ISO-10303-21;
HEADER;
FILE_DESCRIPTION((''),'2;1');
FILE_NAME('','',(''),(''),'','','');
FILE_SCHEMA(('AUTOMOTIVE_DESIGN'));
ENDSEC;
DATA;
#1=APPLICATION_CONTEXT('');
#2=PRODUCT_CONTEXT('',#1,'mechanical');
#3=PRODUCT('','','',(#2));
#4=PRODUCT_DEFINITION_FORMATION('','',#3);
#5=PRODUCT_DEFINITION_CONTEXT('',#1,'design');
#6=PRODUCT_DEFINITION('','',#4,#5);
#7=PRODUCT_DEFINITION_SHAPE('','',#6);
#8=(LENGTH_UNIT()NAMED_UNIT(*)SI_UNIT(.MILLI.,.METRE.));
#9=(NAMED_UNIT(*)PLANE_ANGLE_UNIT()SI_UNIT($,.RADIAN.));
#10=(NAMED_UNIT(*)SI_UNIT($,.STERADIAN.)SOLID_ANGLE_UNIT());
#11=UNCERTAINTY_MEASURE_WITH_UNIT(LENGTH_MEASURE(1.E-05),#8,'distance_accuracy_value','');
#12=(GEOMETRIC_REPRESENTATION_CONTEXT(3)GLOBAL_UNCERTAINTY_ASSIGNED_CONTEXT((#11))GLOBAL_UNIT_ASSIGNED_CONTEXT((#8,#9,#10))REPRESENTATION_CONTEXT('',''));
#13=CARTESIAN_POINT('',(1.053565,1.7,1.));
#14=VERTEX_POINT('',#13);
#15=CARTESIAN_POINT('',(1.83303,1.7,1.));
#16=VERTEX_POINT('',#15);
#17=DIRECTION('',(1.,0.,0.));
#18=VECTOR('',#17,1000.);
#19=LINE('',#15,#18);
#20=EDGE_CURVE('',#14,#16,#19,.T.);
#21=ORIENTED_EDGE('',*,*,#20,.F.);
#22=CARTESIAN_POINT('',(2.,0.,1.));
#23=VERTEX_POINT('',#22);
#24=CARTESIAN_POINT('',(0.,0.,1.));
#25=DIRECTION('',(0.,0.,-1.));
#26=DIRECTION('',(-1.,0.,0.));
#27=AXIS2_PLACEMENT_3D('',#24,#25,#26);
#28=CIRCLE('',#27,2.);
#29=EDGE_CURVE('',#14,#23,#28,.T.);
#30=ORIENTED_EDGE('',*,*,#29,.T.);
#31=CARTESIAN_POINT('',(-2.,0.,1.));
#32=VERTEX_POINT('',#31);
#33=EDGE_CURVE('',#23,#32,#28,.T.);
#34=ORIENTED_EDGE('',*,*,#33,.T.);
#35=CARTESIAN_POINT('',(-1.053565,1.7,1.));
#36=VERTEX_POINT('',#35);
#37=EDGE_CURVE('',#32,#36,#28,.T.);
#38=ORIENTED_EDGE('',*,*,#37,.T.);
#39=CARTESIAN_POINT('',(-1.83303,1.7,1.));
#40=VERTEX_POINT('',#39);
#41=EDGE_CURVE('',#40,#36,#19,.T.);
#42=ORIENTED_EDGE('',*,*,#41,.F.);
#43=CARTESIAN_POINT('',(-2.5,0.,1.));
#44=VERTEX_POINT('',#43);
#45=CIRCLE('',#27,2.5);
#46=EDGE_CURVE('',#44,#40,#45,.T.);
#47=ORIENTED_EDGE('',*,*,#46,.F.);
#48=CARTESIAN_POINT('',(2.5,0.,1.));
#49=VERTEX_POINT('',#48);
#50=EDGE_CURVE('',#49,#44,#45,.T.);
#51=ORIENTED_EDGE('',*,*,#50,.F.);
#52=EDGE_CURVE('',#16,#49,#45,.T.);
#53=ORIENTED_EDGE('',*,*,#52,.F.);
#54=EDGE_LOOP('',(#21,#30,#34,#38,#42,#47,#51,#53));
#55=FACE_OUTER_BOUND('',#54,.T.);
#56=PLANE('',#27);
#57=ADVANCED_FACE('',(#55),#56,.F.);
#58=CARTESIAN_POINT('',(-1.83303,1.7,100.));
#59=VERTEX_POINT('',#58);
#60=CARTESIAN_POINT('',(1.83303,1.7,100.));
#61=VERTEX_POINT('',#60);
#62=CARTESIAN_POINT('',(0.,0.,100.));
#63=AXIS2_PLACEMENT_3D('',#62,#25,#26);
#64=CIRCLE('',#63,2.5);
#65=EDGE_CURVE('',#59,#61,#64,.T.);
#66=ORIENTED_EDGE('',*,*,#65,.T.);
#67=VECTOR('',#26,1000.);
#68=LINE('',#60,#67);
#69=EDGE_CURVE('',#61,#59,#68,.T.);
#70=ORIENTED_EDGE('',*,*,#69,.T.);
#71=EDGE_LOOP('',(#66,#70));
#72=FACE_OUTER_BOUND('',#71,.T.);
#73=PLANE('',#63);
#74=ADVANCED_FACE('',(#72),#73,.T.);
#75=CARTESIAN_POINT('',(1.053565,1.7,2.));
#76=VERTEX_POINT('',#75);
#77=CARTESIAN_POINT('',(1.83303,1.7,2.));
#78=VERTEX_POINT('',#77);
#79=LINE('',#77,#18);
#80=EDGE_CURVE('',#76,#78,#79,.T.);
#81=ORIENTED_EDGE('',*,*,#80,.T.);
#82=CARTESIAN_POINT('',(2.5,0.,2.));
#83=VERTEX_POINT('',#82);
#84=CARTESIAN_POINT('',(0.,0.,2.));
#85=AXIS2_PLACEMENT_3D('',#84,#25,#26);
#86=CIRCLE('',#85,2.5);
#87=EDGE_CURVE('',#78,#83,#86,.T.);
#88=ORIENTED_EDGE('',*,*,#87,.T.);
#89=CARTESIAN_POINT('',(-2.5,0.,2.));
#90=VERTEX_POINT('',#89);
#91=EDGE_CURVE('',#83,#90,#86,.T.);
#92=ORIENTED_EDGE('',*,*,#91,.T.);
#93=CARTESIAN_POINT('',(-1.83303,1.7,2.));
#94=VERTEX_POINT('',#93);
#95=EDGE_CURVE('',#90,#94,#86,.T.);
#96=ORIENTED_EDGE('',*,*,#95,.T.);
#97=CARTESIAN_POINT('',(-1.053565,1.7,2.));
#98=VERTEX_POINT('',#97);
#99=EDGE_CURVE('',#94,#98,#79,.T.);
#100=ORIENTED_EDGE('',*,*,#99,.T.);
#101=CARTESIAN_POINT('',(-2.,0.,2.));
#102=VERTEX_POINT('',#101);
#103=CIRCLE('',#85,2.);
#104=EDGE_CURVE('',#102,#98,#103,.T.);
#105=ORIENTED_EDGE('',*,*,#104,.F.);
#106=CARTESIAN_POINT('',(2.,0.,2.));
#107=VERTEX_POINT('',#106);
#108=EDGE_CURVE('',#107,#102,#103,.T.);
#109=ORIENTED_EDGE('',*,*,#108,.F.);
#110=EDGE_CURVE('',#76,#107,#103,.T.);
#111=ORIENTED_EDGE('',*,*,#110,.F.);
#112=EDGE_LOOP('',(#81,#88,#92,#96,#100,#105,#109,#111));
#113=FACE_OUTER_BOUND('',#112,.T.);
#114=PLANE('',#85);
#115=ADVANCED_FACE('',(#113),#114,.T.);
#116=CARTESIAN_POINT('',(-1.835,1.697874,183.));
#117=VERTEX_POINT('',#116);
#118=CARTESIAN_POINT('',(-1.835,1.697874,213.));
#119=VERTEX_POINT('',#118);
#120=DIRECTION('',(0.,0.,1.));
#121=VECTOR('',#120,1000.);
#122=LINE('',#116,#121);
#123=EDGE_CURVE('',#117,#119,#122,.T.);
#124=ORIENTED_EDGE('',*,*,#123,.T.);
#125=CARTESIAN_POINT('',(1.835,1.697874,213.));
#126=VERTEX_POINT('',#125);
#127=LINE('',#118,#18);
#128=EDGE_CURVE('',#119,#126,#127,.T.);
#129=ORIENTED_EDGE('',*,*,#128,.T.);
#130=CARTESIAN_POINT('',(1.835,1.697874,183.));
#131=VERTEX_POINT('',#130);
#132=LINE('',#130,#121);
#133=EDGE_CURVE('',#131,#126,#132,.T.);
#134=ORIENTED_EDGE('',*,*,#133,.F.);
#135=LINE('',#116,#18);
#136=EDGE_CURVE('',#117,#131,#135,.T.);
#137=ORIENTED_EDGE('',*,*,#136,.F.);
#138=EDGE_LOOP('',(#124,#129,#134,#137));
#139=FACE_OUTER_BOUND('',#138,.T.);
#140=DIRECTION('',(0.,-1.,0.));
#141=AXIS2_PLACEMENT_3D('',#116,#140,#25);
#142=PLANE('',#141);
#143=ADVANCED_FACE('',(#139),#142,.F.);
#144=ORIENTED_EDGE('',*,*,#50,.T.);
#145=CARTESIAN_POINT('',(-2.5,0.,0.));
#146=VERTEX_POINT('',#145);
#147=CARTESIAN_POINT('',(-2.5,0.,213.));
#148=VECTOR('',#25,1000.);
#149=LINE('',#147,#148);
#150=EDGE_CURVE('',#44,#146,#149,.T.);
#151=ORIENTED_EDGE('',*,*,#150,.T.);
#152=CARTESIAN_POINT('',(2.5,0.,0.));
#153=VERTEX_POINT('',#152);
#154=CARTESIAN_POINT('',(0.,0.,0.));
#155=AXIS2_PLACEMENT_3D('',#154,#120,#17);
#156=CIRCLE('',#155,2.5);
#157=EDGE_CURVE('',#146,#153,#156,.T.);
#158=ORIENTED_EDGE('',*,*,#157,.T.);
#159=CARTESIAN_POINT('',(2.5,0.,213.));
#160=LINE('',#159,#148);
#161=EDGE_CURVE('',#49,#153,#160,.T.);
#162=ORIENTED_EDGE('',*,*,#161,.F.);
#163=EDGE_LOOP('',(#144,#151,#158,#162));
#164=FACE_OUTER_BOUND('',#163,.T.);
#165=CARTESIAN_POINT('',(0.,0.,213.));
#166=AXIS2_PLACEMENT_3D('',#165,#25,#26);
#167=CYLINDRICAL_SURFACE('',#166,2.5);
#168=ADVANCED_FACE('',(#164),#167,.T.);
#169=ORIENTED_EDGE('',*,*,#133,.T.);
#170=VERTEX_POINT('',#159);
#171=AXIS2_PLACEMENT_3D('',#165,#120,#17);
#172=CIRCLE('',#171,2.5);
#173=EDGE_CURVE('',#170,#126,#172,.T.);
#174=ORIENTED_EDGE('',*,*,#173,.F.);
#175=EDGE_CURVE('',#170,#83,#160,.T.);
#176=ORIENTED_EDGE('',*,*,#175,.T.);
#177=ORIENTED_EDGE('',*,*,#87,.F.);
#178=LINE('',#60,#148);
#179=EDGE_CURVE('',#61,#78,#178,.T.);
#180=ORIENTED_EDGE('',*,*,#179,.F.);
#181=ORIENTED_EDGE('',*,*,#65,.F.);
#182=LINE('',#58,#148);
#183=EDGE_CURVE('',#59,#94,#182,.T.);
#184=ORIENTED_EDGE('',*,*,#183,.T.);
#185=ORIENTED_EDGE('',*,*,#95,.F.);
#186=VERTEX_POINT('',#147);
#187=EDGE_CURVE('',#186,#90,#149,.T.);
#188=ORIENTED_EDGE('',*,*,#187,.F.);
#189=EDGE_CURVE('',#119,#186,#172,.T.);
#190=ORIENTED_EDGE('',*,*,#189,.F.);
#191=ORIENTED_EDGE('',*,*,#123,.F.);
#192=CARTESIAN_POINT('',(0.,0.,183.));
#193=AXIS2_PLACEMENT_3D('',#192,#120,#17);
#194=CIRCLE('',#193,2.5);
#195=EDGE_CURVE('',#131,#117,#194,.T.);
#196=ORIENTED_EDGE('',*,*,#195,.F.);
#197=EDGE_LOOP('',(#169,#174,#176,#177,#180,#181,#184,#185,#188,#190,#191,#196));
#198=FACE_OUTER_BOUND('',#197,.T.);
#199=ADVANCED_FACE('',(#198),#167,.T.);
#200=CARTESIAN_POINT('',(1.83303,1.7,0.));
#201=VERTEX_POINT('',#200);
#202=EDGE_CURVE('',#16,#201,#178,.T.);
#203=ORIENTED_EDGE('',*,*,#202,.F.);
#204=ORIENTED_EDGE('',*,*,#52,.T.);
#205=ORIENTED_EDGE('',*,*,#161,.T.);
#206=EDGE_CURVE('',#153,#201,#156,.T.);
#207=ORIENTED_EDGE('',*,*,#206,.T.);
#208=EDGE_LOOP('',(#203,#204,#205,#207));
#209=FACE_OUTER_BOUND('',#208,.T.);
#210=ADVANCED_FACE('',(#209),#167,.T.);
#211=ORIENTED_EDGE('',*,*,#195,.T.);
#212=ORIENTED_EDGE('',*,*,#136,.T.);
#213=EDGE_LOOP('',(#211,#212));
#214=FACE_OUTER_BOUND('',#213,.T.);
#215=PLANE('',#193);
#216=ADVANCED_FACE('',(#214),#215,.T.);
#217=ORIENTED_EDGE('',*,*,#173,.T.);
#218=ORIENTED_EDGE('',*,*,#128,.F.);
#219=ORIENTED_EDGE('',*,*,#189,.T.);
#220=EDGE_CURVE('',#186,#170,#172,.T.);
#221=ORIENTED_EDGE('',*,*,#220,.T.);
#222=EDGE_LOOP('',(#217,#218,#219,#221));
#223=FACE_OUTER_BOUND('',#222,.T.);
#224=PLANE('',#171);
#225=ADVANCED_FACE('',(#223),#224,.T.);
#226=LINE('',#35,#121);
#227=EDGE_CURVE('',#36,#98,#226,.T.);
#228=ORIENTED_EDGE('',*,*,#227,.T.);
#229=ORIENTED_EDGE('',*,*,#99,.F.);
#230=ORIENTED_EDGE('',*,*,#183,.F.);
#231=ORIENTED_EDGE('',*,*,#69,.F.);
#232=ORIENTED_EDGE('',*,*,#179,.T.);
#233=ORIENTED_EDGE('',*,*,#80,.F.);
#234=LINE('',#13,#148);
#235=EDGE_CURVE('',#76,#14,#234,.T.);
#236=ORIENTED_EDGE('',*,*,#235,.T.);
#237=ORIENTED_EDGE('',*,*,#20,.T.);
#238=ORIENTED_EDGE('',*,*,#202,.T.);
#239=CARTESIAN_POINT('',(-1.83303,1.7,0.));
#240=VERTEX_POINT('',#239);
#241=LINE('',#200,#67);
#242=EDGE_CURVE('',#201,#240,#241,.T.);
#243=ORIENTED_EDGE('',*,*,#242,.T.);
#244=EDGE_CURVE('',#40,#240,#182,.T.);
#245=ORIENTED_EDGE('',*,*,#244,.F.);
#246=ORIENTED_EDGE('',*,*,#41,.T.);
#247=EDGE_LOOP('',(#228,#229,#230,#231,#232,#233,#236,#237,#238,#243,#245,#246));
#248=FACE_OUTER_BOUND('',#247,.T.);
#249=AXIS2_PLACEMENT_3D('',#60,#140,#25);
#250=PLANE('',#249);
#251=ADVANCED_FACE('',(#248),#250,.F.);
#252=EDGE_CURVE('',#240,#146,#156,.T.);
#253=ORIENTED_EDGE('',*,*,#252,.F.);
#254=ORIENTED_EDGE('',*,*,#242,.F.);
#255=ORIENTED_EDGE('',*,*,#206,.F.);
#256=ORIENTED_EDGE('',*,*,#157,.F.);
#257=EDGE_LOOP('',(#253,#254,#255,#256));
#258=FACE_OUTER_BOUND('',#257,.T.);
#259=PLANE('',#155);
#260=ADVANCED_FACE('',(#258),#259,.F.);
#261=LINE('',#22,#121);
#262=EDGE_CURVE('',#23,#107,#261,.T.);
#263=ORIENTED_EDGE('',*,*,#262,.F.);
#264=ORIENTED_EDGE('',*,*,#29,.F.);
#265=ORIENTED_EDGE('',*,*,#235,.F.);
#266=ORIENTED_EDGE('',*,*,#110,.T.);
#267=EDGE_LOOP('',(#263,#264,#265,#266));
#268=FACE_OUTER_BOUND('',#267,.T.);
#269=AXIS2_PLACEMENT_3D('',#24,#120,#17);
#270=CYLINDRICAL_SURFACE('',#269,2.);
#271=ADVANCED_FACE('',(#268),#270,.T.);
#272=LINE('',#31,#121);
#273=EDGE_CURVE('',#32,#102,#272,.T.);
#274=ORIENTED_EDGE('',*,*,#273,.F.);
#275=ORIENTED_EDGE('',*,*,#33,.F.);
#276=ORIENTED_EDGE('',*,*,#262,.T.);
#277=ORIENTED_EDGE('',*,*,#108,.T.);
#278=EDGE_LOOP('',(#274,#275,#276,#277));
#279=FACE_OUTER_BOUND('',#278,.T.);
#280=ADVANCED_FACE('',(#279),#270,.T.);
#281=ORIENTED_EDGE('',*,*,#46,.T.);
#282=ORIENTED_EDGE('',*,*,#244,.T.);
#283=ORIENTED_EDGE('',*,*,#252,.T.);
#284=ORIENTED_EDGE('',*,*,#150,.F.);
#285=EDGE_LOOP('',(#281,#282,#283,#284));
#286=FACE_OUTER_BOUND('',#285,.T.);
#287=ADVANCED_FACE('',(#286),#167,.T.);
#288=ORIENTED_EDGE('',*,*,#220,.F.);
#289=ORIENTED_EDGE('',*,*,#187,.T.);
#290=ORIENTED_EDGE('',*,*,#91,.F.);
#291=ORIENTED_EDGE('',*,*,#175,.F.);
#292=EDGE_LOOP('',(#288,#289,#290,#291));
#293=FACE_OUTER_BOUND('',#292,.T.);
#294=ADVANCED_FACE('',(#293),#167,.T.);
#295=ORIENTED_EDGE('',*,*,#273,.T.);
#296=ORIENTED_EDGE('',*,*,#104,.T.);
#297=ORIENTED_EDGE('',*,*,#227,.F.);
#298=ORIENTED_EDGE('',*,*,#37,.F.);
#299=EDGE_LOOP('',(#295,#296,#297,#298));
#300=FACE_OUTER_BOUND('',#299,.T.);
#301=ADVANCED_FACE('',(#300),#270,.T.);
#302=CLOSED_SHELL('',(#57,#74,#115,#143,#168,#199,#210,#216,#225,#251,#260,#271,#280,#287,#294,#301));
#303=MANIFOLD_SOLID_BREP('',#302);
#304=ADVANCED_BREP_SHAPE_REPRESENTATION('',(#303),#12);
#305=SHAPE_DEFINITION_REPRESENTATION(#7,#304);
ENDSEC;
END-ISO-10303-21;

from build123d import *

# Parameters (mm, degrees)
SKETCH1_R           = 2.5
BOSS_EXTRUDE1_DEPTH = 213
CUT_EXTRUDE2_DEPTH  = 100
CUT_EXTRUDE3_START  = 1
SKETCH5_R           = 2.5
SKETCH5_R_2         = 2
CUT_EXTRUDE3_DEPTH  = 1
CUT_EXTRUDE4_START  = -30
CUT_EXTRUDE4_DEPTH  = 30


with BuildPart() as part:
    # Sketch1 → Boss-Extrude1 (new body)
    with BuildSketch(Plane.XY):
        Circle(SKETCH1_R)
    extrude(amount=BOSS_EXTRUDE1_DEPTH)

    # Sketch4 → Cut-Extrude2 (cut)
    with BuildSketch(Plane(origin=(0, 0, 0), x_dir=(-1, 0, 0), z_dir=(0, 0, -1))):
        with BuildLine():
            Line((-1.833030278, 1.7), (1.833030278, 1.7))
            ThreePointArc((1.833030278, 1.7), (0, 2.5), (-1.833030278, 1.7))
        make_face()
    extrude(amount=-CUT_EXTRUDE2_DEPTH, mode=Mode.SUBTRACT)

    # Sketch5 → Cut-Extrude3 (cut)
    with BuildSketch(Plane(origin=(0, 0, 2), x_dir=(-1, 0, 0), z_dir=(0, 0, -1)).offset(CUT_EXTRUDE3_START)):
        with Locations(Location((0, 0, 0), (0, 0, 42.843643044))):
            Circle(SKETCH5_R)
        Circle(SKETCH5_R_2, mode=Mode.SUBTRACT)
    extrude(amount=-CUT_EXTRUDE3_DEPTH, mode=Mode.SUBTRACT)

    # Sketch7 → Cut-Extrude4 (cut)
    with BuildSketch(Plane.XY.offset(213).offset(CUT_EXTRUDE4_START)):
        with BuildLine():
            Line((-1.835, 1.69787367), (1.835, 1.69787367))
            ThreePointArc((1.835, 1.69787367), (0, 2.5), (-1.835, 1.69787367))
        make_face()
    extrude(amount=CUT_EXTRUDE4_DEPTH, mode=Mode.SUBTRACT)


solid = part.part
